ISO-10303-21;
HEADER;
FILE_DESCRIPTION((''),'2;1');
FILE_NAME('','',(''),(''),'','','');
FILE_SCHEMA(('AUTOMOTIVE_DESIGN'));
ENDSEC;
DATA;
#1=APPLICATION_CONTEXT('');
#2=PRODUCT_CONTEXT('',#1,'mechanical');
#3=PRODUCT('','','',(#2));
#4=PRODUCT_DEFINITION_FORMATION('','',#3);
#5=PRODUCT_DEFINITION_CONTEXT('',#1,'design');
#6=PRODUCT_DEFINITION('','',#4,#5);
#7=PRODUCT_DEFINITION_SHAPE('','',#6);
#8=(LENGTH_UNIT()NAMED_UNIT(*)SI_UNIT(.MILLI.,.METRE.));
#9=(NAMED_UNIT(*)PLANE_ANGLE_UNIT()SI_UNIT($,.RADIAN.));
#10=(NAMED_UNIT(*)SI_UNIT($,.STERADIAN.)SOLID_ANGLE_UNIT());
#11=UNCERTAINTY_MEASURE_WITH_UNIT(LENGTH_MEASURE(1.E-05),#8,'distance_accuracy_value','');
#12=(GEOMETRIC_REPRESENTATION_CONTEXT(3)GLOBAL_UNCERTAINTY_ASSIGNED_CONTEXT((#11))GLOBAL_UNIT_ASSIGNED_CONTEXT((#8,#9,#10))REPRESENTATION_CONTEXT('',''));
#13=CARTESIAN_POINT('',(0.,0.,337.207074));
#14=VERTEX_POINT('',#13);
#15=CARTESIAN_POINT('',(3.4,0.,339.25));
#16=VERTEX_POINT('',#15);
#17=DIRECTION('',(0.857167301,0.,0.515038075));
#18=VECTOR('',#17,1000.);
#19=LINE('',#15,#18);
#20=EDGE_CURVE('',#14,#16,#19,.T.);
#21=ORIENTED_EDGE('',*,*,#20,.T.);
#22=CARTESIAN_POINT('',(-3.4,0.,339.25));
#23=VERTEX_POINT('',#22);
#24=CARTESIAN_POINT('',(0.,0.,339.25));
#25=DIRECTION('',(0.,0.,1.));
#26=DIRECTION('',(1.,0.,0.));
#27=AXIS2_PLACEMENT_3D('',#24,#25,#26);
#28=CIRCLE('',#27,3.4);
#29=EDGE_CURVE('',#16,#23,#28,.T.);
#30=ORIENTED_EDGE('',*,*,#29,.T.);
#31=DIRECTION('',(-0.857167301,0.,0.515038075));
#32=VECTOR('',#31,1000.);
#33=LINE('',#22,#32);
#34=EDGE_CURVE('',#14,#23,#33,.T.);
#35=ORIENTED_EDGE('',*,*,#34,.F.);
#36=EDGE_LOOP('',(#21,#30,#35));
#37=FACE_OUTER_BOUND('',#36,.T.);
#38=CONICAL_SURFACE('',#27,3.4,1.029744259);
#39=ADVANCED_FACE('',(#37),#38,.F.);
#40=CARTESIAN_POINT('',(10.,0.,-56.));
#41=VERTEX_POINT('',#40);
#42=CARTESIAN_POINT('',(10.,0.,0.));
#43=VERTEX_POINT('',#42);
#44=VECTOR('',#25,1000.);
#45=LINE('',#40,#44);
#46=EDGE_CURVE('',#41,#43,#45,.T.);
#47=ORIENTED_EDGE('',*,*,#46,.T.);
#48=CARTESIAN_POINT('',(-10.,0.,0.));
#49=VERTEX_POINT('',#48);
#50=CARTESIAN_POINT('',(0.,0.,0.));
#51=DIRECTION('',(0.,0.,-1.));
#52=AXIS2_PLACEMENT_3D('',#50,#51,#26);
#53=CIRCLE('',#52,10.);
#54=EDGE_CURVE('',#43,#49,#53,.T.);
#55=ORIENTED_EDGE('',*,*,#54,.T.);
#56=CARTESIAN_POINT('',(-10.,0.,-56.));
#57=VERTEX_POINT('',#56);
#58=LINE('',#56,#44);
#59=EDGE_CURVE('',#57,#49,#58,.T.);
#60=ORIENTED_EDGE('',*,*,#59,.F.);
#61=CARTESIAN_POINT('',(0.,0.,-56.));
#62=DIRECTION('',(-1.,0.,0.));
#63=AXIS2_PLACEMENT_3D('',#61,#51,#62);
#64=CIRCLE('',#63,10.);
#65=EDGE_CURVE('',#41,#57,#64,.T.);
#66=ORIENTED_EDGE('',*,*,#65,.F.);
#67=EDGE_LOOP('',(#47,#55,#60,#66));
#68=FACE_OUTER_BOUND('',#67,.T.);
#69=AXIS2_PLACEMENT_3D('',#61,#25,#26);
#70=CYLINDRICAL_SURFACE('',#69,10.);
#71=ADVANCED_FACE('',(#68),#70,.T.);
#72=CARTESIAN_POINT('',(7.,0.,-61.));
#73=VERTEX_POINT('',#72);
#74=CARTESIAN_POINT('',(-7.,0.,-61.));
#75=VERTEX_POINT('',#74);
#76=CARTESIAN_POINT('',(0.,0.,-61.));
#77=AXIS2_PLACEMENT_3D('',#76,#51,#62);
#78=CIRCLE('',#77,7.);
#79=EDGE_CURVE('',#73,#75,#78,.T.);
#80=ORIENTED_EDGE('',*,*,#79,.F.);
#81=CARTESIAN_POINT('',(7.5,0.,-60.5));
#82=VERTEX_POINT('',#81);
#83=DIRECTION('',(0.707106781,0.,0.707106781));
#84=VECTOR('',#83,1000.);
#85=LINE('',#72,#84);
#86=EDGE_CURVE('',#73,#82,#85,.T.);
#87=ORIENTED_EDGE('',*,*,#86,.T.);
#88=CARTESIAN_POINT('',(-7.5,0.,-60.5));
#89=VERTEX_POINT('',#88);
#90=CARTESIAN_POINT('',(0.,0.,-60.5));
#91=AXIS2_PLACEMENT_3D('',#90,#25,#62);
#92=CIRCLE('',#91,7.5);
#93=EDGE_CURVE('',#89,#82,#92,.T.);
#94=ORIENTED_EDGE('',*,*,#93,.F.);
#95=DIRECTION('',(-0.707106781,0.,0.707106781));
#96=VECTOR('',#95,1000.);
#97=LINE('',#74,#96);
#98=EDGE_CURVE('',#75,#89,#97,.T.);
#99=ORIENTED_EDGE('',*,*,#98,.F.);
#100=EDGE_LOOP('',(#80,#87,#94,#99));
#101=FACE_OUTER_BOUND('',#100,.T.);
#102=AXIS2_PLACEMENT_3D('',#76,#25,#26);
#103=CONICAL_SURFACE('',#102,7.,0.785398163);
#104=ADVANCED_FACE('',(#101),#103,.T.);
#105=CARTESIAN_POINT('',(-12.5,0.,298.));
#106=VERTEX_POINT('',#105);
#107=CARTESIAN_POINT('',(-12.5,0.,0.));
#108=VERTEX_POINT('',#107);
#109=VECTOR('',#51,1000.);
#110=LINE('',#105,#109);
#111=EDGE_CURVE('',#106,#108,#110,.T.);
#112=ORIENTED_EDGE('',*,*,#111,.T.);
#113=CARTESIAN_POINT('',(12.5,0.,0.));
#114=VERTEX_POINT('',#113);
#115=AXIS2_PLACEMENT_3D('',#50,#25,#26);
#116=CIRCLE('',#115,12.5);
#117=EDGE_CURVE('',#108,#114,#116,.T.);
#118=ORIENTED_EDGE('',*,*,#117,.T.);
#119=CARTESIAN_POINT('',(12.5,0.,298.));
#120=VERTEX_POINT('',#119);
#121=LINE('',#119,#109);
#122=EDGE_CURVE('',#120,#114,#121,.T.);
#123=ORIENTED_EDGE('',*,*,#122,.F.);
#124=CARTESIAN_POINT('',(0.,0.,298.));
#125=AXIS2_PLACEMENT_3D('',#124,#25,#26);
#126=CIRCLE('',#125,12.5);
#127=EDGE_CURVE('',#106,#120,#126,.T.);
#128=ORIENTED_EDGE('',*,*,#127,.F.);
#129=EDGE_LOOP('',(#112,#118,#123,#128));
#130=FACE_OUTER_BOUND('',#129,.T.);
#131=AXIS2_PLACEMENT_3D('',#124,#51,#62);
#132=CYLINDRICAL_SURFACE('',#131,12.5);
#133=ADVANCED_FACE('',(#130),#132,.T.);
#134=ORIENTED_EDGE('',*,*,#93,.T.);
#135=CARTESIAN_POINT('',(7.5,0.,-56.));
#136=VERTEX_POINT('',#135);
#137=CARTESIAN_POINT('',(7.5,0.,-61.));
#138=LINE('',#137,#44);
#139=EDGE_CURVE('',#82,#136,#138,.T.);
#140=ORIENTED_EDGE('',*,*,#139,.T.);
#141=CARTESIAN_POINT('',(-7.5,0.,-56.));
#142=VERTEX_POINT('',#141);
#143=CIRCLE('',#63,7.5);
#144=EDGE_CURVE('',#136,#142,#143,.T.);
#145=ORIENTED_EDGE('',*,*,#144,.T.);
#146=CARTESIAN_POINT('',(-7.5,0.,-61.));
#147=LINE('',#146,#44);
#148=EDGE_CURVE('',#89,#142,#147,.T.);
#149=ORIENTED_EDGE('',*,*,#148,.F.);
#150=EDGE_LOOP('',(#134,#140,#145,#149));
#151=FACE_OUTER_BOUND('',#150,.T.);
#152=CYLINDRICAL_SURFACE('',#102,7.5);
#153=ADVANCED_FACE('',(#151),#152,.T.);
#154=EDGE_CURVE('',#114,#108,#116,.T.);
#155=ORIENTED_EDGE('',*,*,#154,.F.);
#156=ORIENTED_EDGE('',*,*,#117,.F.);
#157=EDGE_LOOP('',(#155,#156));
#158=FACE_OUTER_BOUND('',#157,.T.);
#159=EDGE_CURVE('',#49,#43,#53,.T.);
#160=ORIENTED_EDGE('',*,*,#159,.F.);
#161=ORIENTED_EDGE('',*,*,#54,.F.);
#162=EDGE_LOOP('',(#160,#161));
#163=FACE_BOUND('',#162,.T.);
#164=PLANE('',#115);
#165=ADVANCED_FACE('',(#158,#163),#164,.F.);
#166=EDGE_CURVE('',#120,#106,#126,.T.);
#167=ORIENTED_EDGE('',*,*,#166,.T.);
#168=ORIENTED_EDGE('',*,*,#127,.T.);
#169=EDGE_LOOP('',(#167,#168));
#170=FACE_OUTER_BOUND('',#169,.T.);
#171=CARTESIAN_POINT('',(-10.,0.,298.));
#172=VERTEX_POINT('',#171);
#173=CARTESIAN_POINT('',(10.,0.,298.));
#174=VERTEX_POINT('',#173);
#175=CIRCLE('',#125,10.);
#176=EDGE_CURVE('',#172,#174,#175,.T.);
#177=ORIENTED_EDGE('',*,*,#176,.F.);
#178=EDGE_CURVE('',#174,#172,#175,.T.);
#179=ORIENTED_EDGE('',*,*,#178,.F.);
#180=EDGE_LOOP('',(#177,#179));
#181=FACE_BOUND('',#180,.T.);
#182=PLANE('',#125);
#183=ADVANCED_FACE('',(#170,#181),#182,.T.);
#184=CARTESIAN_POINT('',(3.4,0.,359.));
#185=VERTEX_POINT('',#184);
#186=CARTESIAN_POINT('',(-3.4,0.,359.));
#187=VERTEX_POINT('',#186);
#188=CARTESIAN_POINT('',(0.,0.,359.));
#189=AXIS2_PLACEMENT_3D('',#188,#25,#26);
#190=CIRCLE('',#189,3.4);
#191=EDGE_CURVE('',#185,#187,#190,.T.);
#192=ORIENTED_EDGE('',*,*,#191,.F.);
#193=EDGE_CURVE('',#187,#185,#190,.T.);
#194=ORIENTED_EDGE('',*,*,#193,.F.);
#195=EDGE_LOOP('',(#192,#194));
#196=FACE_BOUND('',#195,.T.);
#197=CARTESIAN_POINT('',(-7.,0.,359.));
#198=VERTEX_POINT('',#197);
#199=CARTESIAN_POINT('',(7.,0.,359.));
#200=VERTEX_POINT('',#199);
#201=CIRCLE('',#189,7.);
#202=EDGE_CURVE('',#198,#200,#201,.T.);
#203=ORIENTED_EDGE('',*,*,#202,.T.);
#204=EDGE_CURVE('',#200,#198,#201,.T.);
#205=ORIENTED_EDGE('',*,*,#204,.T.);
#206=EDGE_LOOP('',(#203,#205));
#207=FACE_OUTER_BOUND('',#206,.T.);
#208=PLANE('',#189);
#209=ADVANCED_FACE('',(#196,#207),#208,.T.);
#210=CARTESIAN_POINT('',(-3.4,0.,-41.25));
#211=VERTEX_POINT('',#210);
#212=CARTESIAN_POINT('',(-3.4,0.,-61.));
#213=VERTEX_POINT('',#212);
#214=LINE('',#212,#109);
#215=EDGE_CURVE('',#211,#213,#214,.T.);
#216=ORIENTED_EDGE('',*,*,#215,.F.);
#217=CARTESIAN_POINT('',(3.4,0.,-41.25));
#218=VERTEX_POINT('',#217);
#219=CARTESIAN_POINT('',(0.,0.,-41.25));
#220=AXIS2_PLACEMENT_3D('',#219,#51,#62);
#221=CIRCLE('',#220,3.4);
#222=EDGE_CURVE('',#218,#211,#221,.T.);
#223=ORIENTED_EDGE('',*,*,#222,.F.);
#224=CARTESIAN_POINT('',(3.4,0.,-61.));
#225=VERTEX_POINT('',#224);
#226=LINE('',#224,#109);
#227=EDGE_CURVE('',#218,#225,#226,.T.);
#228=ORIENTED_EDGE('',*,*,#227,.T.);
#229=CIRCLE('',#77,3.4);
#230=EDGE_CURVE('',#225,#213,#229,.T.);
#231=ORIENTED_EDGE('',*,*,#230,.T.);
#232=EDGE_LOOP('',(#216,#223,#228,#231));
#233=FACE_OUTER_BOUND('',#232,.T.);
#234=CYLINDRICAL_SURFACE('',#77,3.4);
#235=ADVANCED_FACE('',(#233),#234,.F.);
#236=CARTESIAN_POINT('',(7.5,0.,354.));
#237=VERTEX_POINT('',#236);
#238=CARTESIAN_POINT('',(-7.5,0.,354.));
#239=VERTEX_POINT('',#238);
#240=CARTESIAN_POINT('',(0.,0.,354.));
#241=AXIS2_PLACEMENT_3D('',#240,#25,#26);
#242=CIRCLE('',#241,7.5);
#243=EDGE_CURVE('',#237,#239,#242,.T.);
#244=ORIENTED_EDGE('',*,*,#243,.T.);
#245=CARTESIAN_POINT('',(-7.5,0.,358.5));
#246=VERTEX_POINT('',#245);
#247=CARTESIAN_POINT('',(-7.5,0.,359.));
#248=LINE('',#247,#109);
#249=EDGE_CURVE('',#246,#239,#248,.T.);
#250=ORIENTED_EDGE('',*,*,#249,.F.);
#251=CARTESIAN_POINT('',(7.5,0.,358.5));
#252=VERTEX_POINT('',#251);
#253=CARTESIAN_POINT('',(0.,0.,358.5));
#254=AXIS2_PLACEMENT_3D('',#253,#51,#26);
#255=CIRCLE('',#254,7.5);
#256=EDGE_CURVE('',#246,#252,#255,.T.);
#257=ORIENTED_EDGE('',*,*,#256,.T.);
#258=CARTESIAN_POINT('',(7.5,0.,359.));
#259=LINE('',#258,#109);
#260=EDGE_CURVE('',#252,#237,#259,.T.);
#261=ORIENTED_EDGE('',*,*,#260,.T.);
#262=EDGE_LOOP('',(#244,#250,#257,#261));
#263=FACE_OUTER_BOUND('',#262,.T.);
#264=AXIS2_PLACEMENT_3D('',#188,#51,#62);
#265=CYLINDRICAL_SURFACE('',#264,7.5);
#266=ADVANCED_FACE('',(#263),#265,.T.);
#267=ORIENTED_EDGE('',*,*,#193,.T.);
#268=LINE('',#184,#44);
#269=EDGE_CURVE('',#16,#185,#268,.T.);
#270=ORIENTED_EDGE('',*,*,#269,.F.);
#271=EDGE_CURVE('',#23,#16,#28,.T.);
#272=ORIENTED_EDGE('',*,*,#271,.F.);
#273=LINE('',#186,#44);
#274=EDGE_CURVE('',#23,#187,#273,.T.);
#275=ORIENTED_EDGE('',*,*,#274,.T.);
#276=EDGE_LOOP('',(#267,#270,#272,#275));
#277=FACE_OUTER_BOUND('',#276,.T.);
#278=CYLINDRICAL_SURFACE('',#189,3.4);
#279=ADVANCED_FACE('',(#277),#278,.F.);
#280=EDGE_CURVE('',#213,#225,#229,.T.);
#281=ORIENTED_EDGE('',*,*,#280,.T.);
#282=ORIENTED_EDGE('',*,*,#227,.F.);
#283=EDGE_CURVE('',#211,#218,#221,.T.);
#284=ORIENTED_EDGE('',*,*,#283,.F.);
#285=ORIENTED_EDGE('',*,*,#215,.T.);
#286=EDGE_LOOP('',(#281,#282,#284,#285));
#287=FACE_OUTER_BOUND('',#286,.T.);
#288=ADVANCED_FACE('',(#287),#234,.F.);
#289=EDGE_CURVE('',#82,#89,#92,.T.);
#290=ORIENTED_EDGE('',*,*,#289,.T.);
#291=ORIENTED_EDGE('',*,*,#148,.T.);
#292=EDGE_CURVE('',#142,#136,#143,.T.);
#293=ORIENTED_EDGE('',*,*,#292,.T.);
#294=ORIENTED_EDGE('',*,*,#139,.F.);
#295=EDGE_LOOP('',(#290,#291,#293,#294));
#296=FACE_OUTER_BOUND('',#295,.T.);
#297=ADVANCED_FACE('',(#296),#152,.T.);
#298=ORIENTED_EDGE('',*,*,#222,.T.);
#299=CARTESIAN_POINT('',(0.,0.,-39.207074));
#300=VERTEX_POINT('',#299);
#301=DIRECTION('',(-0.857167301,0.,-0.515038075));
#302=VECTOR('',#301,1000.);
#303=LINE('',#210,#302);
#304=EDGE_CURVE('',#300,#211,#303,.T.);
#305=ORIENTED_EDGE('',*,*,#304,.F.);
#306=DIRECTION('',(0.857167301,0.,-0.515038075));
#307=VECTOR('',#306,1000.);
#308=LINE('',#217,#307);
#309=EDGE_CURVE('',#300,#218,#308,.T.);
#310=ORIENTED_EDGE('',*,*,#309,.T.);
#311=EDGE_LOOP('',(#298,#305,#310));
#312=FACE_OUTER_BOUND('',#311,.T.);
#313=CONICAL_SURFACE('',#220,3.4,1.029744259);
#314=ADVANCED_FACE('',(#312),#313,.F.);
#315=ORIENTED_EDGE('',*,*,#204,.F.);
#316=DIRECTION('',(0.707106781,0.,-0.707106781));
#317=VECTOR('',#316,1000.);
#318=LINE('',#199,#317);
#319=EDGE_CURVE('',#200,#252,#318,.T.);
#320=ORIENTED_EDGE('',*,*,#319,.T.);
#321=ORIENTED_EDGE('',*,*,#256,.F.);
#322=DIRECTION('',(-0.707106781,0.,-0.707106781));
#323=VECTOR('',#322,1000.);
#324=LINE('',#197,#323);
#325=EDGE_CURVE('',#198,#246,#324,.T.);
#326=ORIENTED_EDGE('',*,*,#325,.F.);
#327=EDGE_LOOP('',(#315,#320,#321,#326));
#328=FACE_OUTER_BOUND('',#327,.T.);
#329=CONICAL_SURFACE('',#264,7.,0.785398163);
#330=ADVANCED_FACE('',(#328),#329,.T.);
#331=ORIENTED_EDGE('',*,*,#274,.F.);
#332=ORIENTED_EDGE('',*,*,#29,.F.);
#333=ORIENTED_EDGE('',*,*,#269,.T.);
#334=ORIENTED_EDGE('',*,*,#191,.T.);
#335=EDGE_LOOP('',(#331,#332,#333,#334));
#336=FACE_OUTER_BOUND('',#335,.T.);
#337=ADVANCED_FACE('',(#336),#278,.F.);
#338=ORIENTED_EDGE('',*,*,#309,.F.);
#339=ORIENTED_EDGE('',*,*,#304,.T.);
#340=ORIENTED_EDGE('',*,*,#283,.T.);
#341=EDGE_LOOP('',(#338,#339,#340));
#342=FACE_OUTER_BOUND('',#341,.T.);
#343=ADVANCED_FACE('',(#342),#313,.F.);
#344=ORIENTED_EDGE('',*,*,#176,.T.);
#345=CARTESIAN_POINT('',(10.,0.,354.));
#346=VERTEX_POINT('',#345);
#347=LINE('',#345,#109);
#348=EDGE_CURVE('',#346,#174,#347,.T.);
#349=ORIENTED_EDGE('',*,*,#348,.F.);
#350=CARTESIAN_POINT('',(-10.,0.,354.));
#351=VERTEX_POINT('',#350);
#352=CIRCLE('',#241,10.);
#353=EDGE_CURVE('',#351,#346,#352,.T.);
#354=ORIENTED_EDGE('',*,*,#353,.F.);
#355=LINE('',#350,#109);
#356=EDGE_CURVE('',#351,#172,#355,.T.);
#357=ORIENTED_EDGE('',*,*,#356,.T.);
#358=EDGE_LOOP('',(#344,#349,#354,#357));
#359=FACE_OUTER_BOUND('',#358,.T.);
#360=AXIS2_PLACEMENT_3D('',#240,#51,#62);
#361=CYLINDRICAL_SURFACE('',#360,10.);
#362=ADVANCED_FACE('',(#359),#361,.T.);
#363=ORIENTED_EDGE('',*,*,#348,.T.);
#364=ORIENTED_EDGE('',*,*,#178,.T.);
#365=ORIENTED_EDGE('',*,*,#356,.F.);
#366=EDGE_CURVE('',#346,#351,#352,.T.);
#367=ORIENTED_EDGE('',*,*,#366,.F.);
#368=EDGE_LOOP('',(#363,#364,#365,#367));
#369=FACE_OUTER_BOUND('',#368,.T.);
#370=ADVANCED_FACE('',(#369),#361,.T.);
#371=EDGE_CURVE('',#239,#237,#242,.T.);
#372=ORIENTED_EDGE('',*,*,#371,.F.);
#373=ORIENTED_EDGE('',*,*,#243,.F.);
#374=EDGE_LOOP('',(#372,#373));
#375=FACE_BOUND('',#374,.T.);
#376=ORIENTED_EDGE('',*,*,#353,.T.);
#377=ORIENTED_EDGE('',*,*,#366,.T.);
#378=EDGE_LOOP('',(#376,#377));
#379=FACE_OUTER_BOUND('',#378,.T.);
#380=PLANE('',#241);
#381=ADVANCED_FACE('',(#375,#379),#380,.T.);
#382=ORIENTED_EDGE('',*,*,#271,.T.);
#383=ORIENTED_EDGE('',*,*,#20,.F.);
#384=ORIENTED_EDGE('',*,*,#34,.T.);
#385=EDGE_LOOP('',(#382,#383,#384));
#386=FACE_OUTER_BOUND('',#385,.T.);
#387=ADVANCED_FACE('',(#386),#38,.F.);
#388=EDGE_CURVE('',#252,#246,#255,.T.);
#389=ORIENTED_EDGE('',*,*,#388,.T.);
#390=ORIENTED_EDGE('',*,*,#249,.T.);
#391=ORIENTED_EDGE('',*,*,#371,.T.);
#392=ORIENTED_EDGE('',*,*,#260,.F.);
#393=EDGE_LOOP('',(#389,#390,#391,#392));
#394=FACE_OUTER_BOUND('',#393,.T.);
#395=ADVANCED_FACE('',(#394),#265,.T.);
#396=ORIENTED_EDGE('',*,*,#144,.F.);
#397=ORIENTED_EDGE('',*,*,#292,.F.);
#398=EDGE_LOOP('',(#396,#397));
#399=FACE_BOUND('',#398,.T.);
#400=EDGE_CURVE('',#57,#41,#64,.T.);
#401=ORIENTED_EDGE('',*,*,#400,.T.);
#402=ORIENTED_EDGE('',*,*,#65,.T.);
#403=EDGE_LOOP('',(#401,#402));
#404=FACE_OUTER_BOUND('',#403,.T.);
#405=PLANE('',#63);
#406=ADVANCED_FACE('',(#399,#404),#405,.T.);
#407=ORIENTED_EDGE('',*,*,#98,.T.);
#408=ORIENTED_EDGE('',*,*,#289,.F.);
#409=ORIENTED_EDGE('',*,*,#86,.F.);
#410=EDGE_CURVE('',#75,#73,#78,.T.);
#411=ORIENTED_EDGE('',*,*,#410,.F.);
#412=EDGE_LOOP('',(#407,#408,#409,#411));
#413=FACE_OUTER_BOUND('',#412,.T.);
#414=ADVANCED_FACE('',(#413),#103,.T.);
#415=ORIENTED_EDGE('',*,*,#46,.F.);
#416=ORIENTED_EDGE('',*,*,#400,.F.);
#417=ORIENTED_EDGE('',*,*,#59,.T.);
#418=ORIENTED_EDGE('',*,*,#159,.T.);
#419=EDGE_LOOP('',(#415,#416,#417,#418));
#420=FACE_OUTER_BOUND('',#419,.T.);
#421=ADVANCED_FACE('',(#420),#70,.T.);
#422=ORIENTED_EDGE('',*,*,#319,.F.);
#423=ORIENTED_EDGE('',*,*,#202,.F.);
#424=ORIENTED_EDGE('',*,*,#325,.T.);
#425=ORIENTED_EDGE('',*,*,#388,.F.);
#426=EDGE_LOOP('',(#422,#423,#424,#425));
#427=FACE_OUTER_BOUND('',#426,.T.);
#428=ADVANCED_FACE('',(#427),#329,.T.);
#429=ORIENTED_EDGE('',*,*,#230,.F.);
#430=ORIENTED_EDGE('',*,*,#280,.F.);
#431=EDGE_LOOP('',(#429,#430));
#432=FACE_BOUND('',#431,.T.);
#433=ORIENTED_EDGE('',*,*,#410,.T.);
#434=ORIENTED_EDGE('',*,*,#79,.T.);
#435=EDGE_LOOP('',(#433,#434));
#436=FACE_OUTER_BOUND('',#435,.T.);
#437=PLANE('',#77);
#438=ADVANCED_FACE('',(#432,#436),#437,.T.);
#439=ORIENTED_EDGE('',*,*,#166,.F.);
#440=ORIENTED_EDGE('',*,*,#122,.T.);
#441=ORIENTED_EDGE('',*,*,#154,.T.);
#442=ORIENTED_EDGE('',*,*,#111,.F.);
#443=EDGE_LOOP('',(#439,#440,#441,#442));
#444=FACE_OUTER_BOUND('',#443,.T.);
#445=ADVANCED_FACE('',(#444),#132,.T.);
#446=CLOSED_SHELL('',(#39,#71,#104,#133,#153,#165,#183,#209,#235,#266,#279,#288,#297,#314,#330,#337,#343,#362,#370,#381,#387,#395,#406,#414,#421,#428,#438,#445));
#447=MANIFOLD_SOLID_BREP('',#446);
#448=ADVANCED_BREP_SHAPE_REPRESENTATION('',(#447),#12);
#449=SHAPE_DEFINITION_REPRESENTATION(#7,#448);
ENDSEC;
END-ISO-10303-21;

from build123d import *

# Parameters (mm, degrees)
SKETCH_1_R             = 12.5
EXTRUDE_1_DEPTH        = 298
SKETCH_2_R             = 10
EXTRUDE_2_DEPTH        = 56
EXTRUDE_START          = 56
SKETCH_3_R             = 10
EXTRUDE_3_DEPTH        = 56
SKETCH_4_R             = 7.5
EXTRUDE_4_DEPTH        = 5
EXTRUDE_START_2        = 5
SKETCH_5_R             = 7.5
EXTRUDE_5_DEPTH        = 5
HOLE_WIZARD_M8_1_D     = 6.8
HOLE_WIZARD_M8_1_DEPTH = 19.75
HOLE_WIZARD_M8_1_TIP   = 2.042926105
HOLE_WIZARD_M8_2_D     = 6.8
HOLE_WIZARD_M8_2_DEPTH = 19.75
HOLE_WIZARD_M8_2_TIP   = 2.042926105
CHAMFER_2_SIZE         = 0.5
CHAMFER_3_SIZE         = 0.5


with BuildPart() as part:
    # 草图1 → 凸台-拉伸1 (new body)
    with BuildSketch(Plane.XY):
        Circle(SKETCH_1_R)
    extrude(amount=EXTRUDE_1_DEPTH)

    # 草图2 → 凸台-拉伸2 (add)
    with BuildSketch(Plane(origin=(0, 0, 0), x_dir=(-1, 0, 0), z_dir=(0, 0, -1))):
        with Locations(Location((0, 0, 0), (0, 0, 180))):
            Circle(SKETCH_2_R)
    extrude(amount=EXTRUDE_2_DEPTH)

    # 草图3 → 凸台-拉伸3 (add)
    with BuildSketch(Plane.XY.offset(298).offset(EXTRUDE_START)):
        Circle(SKETCH_3_R)
    extrude(amount=-EXTRUDE_3_DEPTH)

    # 草图4 → 凸台-拉伸4 (add)
    with BuildSketch(Plane.XY.offset(354)):
        Circle(SKETCH_4_R)
    extrude(amount=EXTRUDE_4_DEPTH)

    # 草图5 → 凸台-拉伸5 (add)
    with BuildSketch(Plane(origin=(0, 0, -56), x_dir=(-1, 0, 0), z_dir=(0, 0, -1)).offset(EXTRUDE_START_2)):
        with Locations(Location((0, 0, 0), (0, 0, 180))):
            Circle(SKETCH_5_R)
    extrude(amount=-EXTRUDE_5_DEPTH)

    # M8 螺纹孔1
    with Locations(Plane(origin=(0, 0, -61), x_dir=(-1, 0, 0), z_dir=(0, 0, -1))):
        with Locations((0, 0)):
            Hole(HOLE_WIZARD_M8_1_D / 2, depth=HOLE_WIZARD_M8_1_DEPTH)
            with Locations((0, 0, -(HOLE_WIZARD_M8_1_DEPTH + HOLE_WIZARD_M8_1_TIP / 2))):  # 118° drill point
                Cone(0, HOLE_WIZARD_M8_1_D / 2, HOLE_WIZARD_M8_1_TIP, mode=Mode.SUBTRACT)

    # M8 螺纹孔2
    with Locations(Plane.XY.offset(359)):
        with Locations((0, 0)):
            Hole(HOLE_WIZARD_M8_2_D / 2, depth=HOLE_WIZARD_M8_2_DEPTH)
            with Locations((0, 0, -(HOLE_WIZARD_M8_2_DEPTH + HOLE_WIZARD_M8_2_TIP / 2))):  # 118° drill point
                Cone(0, HOLE_WIZARD_M8_2_D / 2, HOLE_WIZARD_M8_2_TIP, mode=Mode.SUBTRACT)

    # 倒角2
    chamfer_2_edges = [part.edges().sort_by_distance(p)[0] for p in [
        (-7.5, 0, 359),
    ]]
    chamfer(chamfer_2_edges, length=CHAMFER_2_SIZE)

    # 倒角3
    chamfer_3_edges = [part.edges().sort_by_distance(p)[0] for p in [
        (-7.5, 0, -61),
    ]]
    chamfer(chamfer_3_edges, length=CHAMFER_3_SIZE)


solid = part.part
